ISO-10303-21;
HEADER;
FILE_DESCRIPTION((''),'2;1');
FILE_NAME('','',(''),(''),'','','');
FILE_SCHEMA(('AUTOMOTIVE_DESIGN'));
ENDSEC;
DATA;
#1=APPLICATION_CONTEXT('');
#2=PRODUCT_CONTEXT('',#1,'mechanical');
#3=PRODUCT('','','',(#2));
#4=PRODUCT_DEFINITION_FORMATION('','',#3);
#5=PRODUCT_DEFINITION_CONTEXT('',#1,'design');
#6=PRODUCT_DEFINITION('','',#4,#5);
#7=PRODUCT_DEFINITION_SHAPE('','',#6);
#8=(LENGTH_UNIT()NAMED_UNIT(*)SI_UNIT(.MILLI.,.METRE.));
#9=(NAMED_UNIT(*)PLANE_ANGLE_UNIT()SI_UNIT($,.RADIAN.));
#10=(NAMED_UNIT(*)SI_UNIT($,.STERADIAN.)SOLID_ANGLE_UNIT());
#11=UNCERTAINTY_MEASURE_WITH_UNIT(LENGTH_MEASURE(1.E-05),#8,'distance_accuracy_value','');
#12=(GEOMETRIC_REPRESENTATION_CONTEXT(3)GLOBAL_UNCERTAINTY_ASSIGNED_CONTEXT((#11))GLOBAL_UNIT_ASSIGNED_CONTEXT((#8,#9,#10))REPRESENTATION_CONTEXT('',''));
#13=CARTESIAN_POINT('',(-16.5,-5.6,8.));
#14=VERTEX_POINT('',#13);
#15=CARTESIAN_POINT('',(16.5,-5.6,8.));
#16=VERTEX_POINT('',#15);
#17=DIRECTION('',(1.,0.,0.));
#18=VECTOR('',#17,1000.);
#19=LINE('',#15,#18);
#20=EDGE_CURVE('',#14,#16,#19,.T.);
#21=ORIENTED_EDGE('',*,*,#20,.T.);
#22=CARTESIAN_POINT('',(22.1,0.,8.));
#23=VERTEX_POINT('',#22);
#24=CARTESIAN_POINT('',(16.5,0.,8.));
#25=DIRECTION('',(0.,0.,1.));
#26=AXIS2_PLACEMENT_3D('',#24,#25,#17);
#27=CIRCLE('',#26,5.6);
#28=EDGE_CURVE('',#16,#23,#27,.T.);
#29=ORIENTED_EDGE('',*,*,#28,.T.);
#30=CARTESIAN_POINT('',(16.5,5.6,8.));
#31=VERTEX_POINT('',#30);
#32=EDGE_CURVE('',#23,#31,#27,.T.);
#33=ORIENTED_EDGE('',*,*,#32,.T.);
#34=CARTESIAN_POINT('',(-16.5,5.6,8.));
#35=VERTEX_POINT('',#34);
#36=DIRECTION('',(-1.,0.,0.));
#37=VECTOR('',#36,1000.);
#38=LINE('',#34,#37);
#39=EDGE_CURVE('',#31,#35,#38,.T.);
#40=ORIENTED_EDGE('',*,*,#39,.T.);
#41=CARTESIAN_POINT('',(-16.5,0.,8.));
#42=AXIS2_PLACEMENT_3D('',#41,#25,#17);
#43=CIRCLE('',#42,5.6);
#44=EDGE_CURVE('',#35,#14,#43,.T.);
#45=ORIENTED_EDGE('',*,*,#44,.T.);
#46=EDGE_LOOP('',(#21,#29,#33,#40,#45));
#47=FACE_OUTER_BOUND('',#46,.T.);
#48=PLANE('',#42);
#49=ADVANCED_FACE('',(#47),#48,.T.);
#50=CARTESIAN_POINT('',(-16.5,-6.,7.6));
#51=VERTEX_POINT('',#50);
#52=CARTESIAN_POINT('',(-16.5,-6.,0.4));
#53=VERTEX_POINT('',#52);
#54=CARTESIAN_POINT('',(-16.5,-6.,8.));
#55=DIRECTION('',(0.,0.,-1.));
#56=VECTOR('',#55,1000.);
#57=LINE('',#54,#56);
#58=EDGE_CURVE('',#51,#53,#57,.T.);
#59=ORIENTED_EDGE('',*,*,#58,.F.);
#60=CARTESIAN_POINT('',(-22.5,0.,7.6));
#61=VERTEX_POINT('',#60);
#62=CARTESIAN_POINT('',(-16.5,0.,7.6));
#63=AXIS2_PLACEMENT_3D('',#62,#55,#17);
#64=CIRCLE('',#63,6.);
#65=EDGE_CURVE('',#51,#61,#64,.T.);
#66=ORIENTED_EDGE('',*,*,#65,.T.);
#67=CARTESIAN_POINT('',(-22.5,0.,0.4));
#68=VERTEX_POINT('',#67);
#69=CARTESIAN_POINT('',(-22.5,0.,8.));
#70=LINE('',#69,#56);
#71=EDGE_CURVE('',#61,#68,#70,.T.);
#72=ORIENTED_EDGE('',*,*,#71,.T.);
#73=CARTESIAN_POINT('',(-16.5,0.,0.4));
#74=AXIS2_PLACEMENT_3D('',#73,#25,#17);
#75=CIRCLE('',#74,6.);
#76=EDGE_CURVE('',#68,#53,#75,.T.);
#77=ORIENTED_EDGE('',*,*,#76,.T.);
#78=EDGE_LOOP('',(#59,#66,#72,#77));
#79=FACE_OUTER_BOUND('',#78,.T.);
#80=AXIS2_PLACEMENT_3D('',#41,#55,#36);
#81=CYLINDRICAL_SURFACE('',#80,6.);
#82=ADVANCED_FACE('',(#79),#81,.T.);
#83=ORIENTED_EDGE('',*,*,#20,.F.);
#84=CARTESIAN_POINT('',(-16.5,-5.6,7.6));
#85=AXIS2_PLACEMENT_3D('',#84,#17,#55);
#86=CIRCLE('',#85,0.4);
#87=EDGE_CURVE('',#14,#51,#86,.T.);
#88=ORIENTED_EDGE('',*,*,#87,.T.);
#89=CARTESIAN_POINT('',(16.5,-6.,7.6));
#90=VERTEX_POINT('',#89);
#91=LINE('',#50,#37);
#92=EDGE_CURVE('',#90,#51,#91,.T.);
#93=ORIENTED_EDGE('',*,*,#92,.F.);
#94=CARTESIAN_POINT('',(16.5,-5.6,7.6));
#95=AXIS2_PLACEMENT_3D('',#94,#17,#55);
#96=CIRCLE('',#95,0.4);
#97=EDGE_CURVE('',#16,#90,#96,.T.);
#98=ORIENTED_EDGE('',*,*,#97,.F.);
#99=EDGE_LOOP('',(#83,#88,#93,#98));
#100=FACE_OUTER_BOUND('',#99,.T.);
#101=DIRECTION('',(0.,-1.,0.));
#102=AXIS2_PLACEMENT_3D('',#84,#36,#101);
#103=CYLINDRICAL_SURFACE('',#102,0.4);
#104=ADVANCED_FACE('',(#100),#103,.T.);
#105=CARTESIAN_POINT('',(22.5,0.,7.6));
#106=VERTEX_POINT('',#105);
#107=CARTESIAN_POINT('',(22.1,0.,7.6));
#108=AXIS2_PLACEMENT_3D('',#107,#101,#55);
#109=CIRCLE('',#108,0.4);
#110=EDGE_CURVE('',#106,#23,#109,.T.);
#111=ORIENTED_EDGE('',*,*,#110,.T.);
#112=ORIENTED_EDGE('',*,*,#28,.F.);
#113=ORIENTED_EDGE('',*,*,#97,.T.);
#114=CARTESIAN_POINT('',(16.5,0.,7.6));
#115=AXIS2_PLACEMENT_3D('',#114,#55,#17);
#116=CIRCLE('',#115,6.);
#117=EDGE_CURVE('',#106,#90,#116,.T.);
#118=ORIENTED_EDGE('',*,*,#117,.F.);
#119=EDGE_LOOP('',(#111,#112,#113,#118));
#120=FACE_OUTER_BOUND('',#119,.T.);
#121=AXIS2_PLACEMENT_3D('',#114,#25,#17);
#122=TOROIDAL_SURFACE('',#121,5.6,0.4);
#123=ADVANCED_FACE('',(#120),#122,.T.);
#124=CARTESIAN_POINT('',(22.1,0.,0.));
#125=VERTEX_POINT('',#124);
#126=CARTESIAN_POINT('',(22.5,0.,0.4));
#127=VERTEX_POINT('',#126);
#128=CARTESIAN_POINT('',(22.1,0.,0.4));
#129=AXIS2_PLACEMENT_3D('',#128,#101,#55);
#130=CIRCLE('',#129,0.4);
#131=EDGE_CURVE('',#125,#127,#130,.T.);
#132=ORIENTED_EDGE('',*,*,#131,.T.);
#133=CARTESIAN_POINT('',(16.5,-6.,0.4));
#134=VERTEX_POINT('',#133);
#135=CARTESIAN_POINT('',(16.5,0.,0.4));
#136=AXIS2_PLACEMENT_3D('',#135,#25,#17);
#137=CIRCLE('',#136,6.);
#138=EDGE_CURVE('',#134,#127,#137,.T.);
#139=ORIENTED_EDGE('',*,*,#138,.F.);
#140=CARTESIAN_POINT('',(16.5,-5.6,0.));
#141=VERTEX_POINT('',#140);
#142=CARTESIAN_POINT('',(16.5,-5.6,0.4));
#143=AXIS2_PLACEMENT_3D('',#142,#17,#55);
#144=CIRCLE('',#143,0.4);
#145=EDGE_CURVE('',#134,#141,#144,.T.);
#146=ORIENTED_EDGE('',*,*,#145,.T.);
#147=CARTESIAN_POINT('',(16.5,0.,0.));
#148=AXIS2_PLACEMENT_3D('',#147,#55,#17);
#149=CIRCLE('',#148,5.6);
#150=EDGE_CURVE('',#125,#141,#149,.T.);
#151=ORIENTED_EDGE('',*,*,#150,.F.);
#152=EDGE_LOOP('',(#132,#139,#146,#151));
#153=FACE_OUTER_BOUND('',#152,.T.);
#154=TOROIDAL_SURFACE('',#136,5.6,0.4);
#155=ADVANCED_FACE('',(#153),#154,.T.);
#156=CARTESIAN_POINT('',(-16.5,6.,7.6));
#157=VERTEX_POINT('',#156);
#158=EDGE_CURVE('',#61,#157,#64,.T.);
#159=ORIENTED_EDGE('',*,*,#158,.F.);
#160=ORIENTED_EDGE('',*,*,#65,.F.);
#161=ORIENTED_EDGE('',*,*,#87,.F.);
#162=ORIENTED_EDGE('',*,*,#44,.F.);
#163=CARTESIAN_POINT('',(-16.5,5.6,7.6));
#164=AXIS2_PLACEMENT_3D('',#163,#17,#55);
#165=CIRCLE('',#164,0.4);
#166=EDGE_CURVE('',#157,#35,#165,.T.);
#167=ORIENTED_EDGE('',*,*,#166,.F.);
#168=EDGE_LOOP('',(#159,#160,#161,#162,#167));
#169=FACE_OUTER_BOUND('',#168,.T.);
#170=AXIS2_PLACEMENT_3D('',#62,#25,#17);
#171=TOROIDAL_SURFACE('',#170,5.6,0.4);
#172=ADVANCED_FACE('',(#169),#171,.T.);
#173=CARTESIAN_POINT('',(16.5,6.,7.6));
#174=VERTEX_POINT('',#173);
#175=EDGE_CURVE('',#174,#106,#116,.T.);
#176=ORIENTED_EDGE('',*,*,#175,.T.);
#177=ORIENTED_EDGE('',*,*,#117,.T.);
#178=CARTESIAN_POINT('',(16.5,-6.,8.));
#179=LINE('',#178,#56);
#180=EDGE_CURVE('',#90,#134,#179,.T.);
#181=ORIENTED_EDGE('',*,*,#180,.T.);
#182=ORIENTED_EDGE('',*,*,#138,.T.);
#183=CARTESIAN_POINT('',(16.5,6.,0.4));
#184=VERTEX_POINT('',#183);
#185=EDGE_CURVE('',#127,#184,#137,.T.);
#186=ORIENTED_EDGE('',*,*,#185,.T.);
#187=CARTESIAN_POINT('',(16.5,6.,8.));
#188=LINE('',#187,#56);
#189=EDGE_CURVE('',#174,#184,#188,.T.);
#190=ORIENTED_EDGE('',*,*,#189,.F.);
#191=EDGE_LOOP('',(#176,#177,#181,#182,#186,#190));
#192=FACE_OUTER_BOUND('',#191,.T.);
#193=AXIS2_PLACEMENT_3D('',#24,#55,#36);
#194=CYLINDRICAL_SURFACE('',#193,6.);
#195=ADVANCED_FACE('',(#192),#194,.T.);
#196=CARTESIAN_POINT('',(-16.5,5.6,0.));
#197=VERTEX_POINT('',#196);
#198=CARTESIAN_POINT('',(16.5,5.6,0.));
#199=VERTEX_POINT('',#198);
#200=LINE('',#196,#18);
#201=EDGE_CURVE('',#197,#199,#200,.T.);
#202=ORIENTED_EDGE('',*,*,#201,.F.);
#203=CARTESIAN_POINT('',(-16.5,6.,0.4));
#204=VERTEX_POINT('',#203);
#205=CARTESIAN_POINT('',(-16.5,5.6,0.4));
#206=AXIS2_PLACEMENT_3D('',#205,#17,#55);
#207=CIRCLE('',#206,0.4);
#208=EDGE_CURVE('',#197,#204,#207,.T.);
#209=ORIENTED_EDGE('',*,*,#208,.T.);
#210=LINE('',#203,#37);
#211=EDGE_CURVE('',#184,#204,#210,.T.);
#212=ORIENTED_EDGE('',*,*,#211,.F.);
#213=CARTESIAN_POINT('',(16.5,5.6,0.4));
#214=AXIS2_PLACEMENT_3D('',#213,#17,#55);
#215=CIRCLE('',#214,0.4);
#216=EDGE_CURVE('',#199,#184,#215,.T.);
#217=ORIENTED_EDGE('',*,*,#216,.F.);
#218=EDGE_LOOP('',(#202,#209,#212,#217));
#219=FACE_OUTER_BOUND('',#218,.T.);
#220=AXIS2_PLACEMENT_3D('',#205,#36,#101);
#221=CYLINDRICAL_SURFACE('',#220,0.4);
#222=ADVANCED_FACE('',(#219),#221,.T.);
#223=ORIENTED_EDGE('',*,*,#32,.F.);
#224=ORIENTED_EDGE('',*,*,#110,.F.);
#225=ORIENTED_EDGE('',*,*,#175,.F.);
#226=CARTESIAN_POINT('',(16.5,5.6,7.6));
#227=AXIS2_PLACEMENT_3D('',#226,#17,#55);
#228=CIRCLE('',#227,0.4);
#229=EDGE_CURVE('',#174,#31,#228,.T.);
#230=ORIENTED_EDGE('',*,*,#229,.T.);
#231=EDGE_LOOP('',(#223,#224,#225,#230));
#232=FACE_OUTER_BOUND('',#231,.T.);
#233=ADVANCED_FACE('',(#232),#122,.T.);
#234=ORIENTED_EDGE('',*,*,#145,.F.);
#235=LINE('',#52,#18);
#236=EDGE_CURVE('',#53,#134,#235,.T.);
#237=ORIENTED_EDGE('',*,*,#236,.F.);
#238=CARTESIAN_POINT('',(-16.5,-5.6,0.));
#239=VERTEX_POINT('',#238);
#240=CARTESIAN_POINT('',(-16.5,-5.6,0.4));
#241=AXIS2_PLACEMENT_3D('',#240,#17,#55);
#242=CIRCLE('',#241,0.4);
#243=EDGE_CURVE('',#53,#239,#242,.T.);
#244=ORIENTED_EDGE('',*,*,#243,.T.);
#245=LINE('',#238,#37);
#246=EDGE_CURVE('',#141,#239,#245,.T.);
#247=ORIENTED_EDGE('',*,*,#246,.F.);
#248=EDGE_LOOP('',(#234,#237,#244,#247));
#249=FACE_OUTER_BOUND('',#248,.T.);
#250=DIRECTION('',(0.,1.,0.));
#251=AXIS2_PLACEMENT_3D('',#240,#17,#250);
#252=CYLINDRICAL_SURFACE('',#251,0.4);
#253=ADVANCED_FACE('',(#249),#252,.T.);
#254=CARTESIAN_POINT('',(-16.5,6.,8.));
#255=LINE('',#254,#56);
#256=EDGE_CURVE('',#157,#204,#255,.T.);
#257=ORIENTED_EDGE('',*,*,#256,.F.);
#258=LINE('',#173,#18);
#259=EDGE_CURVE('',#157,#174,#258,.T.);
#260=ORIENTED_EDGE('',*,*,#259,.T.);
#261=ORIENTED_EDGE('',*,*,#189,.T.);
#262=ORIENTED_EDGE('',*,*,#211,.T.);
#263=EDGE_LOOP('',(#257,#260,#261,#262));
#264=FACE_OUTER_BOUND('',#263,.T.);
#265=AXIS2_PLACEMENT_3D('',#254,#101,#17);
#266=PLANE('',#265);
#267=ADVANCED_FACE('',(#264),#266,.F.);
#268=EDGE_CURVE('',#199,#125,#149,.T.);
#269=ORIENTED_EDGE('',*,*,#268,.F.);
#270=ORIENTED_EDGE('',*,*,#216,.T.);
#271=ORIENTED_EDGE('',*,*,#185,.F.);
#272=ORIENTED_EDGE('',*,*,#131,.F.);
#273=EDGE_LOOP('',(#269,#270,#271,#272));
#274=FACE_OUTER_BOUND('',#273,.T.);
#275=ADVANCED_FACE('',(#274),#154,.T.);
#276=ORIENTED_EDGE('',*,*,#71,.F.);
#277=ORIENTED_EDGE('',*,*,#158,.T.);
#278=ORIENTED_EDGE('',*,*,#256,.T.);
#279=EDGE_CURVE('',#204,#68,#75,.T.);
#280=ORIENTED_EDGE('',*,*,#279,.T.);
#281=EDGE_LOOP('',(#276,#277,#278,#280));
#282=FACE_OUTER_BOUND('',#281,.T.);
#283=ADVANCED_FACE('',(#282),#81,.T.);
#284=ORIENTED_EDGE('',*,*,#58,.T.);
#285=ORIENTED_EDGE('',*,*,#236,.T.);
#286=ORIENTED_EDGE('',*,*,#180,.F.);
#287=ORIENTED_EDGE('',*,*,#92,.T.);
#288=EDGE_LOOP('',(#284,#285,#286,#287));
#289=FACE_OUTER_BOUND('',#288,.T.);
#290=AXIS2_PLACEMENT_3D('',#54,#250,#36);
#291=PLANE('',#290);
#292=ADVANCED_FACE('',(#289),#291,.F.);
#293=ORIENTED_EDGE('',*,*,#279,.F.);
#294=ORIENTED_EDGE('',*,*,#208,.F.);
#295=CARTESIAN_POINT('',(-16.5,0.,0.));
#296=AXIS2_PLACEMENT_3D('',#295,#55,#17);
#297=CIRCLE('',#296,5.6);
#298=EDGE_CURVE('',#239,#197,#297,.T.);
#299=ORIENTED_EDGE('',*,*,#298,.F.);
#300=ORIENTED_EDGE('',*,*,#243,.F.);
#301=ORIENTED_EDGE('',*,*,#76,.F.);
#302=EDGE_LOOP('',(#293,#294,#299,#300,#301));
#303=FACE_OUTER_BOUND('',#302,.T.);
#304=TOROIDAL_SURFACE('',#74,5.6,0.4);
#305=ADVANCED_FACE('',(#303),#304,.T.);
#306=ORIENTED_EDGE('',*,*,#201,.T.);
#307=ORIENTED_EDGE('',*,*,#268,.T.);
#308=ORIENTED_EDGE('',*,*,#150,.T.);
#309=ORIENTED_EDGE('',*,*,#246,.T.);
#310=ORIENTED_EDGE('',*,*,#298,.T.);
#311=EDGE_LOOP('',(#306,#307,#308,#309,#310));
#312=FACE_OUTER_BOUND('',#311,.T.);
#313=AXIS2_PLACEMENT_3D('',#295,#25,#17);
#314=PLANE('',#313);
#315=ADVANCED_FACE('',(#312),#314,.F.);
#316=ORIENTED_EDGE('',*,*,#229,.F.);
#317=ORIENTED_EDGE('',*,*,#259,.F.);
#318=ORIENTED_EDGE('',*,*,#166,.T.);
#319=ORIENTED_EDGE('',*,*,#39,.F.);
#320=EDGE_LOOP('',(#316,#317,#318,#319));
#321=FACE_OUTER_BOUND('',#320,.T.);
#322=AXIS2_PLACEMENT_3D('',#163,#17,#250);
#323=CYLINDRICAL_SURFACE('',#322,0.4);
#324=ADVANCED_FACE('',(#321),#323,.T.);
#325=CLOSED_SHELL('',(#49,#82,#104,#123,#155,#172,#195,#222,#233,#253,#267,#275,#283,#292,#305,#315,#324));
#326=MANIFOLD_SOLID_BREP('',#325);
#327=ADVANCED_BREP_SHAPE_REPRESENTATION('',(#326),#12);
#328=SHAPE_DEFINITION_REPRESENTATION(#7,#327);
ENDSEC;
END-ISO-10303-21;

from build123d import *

# Parameters (mm, degrees)
BOSS_EXTRUDE_DEPTH = 8
FILLET1_R          = 0.4


with BuildPart() as part:
    # Sketch1 → Boss-Extrude (new body)
    with BuildSketch(Plane.XY):
        with BuildLine():
            Line((-16.5, 6), (16.5, 6))
            ThreePointArc((16.5, 6), (22.5, 0), (16.5, -6))
            Line((16.5, -6), (-16.5, -6))
            ThreePointArc((-16.5, -6), (-22.5, 0), (-16.5, 6))
        make_face()
    extrude(amount=BOSS_EXTRUDE_DEPTH)

    # Fillet1
    fillet1_edges = [part.edges().sort_by_distance(p)[0] for p in [
        (22.5, 0, 8),
        (0, 6, 8),
        (-22.5, 0, 8),
        (0, 6, 0),
        (22.5, 0, 0),
        (0, -6, 0),
        (-22.5, 0, 0),
        (0, -6, 8),
    ]]
    fillet(fillet1_edges, radius=FILLET1_R)


solid = part.part
